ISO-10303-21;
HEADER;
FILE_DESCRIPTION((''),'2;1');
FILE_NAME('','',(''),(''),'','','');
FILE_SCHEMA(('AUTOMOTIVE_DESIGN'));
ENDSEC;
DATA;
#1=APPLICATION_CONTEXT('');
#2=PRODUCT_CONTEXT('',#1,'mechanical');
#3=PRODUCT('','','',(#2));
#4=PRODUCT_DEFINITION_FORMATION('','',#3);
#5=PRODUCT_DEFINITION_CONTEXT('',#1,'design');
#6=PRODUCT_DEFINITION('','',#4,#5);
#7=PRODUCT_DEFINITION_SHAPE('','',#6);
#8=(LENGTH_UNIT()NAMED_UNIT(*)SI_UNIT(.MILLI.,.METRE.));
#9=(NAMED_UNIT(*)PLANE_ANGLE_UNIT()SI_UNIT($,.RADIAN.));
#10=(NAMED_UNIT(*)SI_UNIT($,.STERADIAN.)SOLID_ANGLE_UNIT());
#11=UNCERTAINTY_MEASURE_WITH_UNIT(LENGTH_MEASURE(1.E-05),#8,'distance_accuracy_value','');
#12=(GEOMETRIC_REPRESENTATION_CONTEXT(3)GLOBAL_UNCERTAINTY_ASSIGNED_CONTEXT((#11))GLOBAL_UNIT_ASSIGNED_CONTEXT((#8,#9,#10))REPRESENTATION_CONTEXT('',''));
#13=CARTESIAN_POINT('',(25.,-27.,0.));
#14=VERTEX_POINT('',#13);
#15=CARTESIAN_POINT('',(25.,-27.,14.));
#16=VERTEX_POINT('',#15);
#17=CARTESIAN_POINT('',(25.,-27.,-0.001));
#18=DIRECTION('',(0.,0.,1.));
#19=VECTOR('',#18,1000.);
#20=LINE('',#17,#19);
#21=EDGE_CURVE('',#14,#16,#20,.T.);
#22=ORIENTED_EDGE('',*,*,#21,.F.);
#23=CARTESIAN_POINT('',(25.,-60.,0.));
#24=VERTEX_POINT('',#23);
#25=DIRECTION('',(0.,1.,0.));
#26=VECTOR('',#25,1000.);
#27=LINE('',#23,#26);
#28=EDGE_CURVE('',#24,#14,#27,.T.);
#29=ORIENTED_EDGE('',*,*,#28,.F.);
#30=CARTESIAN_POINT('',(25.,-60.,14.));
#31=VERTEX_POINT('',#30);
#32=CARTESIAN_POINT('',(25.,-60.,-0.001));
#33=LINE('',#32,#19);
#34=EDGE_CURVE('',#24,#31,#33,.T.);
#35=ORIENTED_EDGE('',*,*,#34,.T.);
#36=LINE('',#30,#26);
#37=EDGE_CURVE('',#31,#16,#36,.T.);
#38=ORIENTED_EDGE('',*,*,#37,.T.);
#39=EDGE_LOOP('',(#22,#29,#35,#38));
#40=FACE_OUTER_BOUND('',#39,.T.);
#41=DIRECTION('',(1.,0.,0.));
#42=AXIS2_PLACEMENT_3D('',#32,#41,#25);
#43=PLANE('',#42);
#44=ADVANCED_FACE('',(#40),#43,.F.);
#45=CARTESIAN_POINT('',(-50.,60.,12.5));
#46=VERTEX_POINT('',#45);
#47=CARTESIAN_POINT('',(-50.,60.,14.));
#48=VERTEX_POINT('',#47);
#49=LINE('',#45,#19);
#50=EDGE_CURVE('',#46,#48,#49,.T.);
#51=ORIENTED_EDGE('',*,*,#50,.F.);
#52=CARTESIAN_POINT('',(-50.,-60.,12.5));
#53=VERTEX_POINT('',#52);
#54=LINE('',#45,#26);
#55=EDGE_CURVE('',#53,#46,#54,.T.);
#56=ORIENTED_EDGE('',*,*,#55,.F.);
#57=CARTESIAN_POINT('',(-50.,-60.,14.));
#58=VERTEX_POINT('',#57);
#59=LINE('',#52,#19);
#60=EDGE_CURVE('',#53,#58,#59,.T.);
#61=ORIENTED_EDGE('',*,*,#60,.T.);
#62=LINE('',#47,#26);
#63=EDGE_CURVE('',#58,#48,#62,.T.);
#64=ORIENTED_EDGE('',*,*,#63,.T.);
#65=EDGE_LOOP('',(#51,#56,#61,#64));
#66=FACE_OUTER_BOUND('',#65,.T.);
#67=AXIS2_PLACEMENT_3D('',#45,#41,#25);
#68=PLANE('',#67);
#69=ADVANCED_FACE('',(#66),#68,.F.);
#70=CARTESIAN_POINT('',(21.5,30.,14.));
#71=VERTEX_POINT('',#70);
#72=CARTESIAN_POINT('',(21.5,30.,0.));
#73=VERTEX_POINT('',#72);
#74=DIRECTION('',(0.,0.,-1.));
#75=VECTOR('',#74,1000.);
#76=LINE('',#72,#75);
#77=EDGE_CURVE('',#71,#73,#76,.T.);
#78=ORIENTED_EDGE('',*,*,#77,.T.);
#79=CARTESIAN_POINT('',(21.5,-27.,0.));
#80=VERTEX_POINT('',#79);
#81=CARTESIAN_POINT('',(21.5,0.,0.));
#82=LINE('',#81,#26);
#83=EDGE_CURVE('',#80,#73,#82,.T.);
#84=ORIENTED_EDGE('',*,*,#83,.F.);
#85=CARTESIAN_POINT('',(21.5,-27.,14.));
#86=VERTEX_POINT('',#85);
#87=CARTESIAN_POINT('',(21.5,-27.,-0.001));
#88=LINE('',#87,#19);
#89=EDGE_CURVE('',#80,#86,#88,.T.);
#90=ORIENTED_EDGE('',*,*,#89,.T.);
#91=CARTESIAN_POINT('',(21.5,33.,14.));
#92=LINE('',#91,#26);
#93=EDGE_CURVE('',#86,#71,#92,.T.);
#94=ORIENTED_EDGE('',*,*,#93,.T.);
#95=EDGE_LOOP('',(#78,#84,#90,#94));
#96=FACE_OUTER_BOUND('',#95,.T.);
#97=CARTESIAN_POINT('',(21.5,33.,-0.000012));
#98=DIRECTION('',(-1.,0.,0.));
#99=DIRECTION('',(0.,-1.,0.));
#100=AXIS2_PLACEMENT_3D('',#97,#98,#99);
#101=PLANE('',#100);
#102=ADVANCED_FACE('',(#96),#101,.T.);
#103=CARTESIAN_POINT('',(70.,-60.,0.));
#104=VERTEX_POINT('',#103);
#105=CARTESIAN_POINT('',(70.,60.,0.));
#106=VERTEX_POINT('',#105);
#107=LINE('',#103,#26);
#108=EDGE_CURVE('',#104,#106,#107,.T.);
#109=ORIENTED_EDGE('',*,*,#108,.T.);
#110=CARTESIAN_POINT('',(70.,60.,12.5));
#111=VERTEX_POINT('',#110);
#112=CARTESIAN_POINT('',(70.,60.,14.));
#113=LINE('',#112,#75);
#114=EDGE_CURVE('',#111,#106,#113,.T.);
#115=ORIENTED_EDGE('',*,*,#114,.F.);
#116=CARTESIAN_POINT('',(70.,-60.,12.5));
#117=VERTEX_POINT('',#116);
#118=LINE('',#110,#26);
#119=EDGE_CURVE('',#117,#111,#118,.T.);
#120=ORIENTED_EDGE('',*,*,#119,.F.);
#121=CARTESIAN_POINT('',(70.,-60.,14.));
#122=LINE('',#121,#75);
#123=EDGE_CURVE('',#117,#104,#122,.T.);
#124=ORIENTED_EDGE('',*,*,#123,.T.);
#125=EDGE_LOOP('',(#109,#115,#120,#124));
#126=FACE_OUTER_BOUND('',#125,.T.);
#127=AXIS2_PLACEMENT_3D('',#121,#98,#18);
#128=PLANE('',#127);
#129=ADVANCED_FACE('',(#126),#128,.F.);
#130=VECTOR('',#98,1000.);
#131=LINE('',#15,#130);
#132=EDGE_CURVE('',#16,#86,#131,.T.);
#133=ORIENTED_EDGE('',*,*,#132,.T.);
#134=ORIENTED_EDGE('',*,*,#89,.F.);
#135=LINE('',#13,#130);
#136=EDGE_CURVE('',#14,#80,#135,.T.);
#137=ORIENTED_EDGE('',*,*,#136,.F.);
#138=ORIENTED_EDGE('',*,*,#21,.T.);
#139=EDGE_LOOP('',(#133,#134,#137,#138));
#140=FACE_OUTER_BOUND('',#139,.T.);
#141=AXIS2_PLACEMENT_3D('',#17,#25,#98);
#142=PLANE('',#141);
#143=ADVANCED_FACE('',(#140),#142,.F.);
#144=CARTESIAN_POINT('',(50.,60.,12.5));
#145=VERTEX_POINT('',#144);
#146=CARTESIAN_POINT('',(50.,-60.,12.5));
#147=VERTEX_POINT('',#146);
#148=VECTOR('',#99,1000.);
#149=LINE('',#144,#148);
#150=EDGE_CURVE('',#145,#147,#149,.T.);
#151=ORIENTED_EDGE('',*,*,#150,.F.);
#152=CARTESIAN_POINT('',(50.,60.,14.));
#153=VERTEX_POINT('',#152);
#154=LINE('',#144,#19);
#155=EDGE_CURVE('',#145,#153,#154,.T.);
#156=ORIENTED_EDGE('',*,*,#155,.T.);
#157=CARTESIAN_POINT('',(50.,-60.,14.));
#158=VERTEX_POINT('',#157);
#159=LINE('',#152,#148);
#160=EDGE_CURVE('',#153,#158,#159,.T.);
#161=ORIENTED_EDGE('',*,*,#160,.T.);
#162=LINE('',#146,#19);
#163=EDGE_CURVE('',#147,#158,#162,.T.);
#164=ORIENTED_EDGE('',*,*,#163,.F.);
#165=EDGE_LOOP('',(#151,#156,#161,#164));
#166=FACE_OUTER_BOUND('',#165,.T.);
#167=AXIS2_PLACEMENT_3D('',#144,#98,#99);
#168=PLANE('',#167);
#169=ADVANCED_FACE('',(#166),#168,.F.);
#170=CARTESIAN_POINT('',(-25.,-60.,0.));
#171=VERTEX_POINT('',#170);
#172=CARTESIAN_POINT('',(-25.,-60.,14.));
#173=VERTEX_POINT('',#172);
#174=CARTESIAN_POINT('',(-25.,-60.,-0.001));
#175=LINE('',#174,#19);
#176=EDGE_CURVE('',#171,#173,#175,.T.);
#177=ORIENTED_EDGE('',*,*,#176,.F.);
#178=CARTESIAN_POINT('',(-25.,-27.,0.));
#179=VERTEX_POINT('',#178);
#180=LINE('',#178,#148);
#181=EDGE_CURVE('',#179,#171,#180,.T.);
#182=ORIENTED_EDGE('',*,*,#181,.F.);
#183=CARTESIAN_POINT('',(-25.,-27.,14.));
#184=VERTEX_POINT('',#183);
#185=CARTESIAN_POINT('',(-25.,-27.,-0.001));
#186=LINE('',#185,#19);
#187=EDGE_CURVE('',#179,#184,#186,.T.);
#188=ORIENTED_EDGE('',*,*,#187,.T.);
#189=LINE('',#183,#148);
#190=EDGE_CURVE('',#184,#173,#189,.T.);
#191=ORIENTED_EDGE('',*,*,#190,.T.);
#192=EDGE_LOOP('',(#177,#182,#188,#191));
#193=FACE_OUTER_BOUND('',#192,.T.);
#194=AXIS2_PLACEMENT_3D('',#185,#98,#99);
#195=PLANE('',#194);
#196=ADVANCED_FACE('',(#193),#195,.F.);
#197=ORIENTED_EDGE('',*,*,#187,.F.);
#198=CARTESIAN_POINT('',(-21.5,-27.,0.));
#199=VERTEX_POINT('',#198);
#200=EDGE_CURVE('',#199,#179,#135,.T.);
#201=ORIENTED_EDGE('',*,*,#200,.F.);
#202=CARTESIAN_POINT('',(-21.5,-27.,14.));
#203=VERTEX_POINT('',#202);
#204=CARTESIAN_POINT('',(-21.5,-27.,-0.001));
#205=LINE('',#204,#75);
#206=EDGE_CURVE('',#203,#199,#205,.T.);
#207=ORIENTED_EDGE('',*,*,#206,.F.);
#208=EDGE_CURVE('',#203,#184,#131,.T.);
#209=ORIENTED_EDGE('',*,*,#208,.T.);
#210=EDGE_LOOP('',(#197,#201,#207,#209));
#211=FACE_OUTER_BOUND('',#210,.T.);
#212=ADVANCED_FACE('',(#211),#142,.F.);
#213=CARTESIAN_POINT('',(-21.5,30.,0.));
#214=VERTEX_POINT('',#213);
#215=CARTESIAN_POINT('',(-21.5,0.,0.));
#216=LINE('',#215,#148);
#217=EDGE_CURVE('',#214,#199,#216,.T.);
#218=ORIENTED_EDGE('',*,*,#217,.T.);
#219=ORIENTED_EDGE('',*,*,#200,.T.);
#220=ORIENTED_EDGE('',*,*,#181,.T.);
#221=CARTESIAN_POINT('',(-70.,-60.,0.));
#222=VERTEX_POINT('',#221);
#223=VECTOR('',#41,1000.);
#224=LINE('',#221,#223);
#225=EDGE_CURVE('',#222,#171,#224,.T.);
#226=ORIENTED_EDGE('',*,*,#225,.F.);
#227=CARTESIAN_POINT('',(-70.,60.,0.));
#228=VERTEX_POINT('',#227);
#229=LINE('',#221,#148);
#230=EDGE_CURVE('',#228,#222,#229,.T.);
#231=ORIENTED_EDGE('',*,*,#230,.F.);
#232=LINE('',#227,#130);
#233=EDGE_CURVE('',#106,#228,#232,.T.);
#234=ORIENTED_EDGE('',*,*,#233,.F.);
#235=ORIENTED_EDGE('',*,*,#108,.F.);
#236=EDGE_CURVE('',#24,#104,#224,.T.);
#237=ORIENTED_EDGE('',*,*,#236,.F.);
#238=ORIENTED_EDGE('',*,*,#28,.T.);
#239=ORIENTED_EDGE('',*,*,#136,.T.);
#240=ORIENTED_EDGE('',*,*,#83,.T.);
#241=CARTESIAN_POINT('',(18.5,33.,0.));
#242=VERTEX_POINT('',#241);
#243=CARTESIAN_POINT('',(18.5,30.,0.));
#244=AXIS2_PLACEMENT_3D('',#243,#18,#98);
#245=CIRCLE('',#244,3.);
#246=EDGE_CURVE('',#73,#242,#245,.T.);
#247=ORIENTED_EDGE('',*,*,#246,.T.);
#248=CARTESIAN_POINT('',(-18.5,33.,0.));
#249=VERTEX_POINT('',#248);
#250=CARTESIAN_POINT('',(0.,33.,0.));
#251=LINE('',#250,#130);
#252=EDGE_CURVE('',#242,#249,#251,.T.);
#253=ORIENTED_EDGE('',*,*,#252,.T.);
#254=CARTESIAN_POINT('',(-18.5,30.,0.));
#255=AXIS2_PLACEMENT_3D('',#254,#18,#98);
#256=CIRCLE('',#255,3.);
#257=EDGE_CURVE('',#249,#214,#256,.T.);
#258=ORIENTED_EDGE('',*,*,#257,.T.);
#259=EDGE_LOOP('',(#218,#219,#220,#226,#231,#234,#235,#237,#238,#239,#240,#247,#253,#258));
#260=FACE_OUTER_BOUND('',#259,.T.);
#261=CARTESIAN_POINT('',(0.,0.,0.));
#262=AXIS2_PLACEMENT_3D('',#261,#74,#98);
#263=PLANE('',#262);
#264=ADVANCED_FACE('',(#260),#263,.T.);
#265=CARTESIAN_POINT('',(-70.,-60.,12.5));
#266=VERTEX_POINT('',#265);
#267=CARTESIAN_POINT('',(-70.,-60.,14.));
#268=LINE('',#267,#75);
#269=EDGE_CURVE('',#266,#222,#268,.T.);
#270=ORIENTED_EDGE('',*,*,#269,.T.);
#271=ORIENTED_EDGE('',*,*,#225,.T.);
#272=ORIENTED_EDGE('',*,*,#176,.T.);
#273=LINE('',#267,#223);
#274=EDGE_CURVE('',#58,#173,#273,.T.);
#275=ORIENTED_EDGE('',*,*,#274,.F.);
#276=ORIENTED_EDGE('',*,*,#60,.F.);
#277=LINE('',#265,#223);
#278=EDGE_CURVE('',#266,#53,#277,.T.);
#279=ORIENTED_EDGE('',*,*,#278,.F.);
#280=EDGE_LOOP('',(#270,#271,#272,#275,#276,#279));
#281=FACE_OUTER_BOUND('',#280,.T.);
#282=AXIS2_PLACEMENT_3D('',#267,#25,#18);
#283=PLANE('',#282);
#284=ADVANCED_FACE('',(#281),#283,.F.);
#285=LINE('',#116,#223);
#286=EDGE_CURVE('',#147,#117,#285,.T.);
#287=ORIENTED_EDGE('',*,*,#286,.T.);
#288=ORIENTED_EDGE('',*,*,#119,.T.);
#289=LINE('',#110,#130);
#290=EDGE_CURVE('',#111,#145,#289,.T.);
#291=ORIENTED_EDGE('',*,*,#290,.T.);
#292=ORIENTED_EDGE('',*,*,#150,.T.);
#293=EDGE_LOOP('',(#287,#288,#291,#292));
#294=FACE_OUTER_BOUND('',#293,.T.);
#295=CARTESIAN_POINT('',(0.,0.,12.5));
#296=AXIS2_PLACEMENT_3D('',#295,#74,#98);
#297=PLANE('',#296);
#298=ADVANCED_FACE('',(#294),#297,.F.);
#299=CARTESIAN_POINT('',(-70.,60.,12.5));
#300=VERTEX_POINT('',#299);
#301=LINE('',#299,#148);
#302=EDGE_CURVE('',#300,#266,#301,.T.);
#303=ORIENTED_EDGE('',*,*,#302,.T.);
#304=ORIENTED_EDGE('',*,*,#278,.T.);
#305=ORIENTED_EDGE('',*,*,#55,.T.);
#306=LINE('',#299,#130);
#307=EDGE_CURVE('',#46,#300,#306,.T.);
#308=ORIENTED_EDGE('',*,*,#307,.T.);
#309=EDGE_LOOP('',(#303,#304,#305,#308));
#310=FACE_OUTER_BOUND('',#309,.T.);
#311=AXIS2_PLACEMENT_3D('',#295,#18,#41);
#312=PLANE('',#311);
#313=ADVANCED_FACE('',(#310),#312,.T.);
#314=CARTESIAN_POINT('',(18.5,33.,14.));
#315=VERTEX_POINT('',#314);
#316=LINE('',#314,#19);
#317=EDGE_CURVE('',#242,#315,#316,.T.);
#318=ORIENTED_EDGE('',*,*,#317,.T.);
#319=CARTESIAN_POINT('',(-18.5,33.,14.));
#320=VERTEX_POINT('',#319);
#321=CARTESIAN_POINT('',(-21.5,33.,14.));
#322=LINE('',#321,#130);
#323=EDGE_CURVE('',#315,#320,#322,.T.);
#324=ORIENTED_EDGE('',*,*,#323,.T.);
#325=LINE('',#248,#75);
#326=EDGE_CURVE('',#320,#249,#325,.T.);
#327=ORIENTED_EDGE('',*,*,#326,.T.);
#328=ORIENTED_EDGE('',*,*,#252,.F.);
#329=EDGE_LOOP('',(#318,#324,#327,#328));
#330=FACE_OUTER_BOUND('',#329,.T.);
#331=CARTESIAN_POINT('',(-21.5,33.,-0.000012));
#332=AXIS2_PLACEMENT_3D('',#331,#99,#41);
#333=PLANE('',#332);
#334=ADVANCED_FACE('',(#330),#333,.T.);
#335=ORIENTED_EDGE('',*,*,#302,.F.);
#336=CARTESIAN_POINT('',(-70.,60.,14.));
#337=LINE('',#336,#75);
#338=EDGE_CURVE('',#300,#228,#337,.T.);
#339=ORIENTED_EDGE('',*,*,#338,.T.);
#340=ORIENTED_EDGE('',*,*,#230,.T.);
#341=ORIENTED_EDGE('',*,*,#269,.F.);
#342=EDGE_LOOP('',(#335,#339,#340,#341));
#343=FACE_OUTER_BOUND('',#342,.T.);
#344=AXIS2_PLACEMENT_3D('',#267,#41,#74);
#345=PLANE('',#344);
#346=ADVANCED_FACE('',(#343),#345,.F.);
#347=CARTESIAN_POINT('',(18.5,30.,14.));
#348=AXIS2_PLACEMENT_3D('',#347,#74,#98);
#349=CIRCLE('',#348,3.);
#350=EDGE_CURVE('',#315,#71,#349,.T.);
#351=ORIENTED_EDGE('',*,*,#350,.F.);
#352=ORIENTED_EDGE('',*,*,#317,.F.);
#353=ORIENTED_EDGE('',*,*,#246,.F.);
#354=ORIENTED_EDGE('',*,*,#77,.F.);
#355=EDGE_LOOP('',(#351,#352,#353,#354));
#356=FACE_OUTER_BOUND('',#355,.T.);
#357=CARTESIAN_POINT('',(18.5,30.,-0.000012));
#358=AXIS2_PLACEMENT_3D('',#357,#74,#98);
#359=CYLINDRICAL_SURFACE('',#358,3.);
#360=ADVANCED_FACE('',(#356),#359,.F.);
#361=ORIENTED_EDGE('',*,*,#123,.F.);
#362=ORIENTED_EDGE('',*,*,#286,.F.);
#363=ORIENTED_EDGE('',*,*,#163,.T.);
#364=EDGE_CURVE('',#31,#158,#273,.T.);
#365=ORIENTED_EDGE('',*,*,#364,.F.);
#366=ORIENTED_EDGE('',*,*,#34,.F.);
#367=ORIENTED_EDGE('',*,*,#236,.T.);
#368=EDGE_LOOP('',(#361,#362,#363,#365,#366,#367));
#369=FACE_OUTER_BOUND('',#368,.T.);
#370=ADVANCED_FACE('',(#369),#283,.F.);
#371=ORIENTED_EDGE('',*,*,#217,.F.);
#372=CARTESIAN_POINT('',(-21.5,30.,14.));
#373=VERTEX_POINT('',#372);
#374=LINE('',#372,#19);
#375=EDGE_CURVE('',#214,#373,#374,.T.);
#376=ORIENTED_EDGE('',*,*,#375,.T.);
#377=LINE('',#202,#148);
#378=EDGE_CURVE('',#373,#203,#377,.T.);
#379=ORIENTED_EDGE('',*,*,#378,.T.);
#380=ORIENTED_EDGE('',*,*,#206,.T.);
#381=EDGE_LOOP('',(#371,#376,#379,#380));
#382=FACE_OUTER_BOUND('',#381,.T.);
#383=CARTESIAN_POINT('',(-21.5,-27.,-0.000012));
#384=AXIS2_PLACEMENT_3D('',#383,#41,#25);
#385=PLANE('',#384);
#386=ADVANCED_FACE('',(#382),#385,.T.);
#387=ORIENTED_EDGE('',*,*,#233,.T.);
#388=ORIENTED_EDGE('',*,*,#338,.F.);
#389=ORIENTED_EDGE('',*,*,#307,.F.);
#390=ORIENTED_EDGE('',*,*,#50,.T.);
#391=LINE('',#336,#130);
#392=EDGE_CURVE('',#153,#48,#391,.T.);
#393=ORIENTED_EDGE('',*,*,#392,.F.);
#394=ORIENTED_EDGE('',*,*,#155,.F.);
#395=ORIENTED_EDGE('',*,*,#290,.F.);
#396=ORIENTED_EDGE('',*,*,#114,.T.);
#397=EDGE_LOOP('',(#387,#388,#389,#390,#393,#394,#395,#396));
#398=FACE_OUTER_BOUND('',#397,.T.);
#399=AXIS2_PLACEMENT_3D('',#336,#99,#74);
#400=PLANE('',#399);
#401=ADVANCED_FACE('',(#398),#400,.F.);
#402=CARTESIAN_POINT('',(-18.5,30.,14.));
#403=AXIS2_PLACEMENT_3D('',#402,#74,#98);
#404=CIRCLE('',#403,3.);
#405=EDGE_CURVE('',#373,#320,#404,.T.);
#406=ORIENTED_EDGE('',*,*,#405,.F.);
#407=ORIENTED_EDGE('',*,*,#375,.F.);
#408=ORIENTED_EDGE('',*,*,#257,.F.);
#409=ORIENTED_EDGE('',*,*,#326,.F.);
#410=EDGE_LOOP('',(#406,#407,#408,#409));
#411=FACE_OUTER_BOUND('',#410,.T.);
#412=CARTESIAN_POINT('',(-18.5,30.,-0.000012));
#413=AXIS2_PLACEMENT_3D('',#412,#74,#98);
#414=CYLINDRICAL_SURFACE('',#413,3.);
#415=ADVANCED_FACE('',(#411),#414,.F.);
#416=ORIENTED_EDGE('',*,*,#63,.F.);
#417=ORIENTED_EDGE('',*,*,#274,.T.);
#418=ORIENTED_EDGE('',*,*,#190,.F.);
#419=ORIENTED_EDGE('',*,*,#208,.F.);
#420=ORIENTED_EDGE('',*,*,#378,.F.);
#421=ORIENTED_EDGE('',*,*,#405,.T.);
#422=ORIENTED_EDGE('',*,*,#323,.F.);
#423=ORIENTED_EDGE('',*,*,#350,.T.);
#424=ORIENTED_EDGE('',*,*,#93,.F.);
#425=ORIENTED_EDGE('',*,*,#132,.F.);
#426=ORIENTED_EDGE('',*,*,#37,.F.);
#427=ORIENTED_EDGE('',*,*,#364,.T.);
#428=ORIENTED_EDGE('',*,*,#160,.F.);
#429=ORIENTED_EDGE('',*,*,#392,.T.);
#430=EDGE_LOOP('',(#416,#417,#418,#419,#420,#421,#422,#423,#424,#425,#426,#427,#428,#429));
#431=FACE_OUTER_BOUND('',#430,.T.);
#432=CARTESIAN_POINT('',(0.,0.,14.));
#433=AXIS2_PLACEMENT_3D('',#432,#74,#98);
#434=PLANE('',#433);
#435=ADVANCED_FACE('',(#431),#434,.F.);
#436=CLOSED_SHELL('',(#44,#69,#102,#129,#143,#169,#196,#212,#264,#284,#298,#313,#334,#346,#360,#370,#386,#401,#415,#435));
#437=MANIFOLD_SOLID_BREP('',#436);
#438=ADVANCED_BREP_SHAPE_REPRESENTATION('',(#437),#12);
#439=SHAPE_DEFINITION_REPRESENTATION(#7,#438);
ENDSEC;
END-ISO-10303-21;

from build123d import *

# Parameters (mm, degrees)
SKETCH_1_W                      = 140
SKETCH_1_H                      = 120
EXTRUDE_1_DEPTH                 = 14
SKETCH_2_W                      = 20
SKETCH_2_H                      = 120
CUT_EXTRUDE_1_DEPTH             = 1.5
CUT_EXTRUDE_2_REACH             = 95.252
SKETCH_3_W                      = 50
SKETCH_3_H                      = 33
CUT_EXTRUDE_3_REACH             = 95.252
SKETCH_4_W                      = 43
SKETCH_4_H                      = 60
CUT_EXTRUDE_3_DIRECTION_2_DEPTH = 94.252345815
FILLET_1_R                      = 3


with BuildPart() as part:
    # 草图1 → 凸台-拉伸1 (new body)
    with BuildSketch(Plane.XY):
        Rectangle(SKETCH_1_W, SKETCH_1_H)
    extrude(amount=EXTRUDE_1_DEPTH)

    # 草图2 → 切除-拉伸1 (cut)
    with BuildSketch(Plane.XY.offset(14)):
        with Locations((-60, 0)):
            Rectangle(SKETCH_2_W, SKETCH_2_H)
        with Locations((60, 0)):
            Rectangle(SKETCH_2_W, SKETCH_2_H)
    extrude(amount=-CUT_EXTRUDE_1_DEPTH, mode=Mode.SUBTRACT)

    # 草图3 → 切除-拉伸2 (cut, up to next)
    with BuildSketch(Plane.XY.offset(14), mode=Mode.PRIVATE) as cut_extrude_2_sk1:
        with Locations((0, -43.5)):
            Rectangle(SKETCH_3_W, SKETCH_3_H)
    cut_extrude_2_tool1 = extrude(cut_extrude_2_sk1.sketch, amount=-CUT_EXTRUDE_2_REACH, mode=Mode.PRIVATE) & part.part
    add(cut_extrude_2_tool1.solids().sort_by_distance((0, -43.5, 14))[0], mode=Mode.SUBTRACT)

    # 草图4 → 切除-拉伸3 (cut, up to next)
    with BuildSketch(Plane(origin=(0, 0, 0), x_dir=(-1, 0, 0), z_dir=(0, 0, -1)), mode=Mode.PRIVATE) as cut_extrude_3_sk1:
        with Locations((0, 3)):
            Rectangle(SKETCH_4_W, SKETCH_4_H)
    cut_extrude_3_tool1 = extrude(cut_extrude_3_sk1.sketch, amount=-CUT_EXTRUDE_3_REACH, mode=Mode.PRIVATE) & part.part
    add(cut_extrude_3_tool1.solids().sort_by_distance((0, 3, 0))[0], mode=Mode.SUBTRACT)

    # 草图4 → 切除-拉伸3 direction 2 (cut)
    with BuildSketch(Plane(origin=(0, 0, 0), x_dir=(-1, 0, 0), z_dir=(0, 0, -1))):
        with Locations((0, 3)):
            Rectangle(SKETCH_4_W, SKETCH_4_H)
    extrude(amount=CUT_EXTRUDE_3_DIRECTION_2_DEPTH, mode=Mode.SUBTRACT)

    # 圆角1
    fillet_1_edges = [part.edges().sort_by_distance(p)[0] for p in [
        (-21.5, 33, 7),
        (21.5, 33, 7),
    ]]
    fillet(fillet_1_edges, radius=FILLET_1_R)


solid = part.part
